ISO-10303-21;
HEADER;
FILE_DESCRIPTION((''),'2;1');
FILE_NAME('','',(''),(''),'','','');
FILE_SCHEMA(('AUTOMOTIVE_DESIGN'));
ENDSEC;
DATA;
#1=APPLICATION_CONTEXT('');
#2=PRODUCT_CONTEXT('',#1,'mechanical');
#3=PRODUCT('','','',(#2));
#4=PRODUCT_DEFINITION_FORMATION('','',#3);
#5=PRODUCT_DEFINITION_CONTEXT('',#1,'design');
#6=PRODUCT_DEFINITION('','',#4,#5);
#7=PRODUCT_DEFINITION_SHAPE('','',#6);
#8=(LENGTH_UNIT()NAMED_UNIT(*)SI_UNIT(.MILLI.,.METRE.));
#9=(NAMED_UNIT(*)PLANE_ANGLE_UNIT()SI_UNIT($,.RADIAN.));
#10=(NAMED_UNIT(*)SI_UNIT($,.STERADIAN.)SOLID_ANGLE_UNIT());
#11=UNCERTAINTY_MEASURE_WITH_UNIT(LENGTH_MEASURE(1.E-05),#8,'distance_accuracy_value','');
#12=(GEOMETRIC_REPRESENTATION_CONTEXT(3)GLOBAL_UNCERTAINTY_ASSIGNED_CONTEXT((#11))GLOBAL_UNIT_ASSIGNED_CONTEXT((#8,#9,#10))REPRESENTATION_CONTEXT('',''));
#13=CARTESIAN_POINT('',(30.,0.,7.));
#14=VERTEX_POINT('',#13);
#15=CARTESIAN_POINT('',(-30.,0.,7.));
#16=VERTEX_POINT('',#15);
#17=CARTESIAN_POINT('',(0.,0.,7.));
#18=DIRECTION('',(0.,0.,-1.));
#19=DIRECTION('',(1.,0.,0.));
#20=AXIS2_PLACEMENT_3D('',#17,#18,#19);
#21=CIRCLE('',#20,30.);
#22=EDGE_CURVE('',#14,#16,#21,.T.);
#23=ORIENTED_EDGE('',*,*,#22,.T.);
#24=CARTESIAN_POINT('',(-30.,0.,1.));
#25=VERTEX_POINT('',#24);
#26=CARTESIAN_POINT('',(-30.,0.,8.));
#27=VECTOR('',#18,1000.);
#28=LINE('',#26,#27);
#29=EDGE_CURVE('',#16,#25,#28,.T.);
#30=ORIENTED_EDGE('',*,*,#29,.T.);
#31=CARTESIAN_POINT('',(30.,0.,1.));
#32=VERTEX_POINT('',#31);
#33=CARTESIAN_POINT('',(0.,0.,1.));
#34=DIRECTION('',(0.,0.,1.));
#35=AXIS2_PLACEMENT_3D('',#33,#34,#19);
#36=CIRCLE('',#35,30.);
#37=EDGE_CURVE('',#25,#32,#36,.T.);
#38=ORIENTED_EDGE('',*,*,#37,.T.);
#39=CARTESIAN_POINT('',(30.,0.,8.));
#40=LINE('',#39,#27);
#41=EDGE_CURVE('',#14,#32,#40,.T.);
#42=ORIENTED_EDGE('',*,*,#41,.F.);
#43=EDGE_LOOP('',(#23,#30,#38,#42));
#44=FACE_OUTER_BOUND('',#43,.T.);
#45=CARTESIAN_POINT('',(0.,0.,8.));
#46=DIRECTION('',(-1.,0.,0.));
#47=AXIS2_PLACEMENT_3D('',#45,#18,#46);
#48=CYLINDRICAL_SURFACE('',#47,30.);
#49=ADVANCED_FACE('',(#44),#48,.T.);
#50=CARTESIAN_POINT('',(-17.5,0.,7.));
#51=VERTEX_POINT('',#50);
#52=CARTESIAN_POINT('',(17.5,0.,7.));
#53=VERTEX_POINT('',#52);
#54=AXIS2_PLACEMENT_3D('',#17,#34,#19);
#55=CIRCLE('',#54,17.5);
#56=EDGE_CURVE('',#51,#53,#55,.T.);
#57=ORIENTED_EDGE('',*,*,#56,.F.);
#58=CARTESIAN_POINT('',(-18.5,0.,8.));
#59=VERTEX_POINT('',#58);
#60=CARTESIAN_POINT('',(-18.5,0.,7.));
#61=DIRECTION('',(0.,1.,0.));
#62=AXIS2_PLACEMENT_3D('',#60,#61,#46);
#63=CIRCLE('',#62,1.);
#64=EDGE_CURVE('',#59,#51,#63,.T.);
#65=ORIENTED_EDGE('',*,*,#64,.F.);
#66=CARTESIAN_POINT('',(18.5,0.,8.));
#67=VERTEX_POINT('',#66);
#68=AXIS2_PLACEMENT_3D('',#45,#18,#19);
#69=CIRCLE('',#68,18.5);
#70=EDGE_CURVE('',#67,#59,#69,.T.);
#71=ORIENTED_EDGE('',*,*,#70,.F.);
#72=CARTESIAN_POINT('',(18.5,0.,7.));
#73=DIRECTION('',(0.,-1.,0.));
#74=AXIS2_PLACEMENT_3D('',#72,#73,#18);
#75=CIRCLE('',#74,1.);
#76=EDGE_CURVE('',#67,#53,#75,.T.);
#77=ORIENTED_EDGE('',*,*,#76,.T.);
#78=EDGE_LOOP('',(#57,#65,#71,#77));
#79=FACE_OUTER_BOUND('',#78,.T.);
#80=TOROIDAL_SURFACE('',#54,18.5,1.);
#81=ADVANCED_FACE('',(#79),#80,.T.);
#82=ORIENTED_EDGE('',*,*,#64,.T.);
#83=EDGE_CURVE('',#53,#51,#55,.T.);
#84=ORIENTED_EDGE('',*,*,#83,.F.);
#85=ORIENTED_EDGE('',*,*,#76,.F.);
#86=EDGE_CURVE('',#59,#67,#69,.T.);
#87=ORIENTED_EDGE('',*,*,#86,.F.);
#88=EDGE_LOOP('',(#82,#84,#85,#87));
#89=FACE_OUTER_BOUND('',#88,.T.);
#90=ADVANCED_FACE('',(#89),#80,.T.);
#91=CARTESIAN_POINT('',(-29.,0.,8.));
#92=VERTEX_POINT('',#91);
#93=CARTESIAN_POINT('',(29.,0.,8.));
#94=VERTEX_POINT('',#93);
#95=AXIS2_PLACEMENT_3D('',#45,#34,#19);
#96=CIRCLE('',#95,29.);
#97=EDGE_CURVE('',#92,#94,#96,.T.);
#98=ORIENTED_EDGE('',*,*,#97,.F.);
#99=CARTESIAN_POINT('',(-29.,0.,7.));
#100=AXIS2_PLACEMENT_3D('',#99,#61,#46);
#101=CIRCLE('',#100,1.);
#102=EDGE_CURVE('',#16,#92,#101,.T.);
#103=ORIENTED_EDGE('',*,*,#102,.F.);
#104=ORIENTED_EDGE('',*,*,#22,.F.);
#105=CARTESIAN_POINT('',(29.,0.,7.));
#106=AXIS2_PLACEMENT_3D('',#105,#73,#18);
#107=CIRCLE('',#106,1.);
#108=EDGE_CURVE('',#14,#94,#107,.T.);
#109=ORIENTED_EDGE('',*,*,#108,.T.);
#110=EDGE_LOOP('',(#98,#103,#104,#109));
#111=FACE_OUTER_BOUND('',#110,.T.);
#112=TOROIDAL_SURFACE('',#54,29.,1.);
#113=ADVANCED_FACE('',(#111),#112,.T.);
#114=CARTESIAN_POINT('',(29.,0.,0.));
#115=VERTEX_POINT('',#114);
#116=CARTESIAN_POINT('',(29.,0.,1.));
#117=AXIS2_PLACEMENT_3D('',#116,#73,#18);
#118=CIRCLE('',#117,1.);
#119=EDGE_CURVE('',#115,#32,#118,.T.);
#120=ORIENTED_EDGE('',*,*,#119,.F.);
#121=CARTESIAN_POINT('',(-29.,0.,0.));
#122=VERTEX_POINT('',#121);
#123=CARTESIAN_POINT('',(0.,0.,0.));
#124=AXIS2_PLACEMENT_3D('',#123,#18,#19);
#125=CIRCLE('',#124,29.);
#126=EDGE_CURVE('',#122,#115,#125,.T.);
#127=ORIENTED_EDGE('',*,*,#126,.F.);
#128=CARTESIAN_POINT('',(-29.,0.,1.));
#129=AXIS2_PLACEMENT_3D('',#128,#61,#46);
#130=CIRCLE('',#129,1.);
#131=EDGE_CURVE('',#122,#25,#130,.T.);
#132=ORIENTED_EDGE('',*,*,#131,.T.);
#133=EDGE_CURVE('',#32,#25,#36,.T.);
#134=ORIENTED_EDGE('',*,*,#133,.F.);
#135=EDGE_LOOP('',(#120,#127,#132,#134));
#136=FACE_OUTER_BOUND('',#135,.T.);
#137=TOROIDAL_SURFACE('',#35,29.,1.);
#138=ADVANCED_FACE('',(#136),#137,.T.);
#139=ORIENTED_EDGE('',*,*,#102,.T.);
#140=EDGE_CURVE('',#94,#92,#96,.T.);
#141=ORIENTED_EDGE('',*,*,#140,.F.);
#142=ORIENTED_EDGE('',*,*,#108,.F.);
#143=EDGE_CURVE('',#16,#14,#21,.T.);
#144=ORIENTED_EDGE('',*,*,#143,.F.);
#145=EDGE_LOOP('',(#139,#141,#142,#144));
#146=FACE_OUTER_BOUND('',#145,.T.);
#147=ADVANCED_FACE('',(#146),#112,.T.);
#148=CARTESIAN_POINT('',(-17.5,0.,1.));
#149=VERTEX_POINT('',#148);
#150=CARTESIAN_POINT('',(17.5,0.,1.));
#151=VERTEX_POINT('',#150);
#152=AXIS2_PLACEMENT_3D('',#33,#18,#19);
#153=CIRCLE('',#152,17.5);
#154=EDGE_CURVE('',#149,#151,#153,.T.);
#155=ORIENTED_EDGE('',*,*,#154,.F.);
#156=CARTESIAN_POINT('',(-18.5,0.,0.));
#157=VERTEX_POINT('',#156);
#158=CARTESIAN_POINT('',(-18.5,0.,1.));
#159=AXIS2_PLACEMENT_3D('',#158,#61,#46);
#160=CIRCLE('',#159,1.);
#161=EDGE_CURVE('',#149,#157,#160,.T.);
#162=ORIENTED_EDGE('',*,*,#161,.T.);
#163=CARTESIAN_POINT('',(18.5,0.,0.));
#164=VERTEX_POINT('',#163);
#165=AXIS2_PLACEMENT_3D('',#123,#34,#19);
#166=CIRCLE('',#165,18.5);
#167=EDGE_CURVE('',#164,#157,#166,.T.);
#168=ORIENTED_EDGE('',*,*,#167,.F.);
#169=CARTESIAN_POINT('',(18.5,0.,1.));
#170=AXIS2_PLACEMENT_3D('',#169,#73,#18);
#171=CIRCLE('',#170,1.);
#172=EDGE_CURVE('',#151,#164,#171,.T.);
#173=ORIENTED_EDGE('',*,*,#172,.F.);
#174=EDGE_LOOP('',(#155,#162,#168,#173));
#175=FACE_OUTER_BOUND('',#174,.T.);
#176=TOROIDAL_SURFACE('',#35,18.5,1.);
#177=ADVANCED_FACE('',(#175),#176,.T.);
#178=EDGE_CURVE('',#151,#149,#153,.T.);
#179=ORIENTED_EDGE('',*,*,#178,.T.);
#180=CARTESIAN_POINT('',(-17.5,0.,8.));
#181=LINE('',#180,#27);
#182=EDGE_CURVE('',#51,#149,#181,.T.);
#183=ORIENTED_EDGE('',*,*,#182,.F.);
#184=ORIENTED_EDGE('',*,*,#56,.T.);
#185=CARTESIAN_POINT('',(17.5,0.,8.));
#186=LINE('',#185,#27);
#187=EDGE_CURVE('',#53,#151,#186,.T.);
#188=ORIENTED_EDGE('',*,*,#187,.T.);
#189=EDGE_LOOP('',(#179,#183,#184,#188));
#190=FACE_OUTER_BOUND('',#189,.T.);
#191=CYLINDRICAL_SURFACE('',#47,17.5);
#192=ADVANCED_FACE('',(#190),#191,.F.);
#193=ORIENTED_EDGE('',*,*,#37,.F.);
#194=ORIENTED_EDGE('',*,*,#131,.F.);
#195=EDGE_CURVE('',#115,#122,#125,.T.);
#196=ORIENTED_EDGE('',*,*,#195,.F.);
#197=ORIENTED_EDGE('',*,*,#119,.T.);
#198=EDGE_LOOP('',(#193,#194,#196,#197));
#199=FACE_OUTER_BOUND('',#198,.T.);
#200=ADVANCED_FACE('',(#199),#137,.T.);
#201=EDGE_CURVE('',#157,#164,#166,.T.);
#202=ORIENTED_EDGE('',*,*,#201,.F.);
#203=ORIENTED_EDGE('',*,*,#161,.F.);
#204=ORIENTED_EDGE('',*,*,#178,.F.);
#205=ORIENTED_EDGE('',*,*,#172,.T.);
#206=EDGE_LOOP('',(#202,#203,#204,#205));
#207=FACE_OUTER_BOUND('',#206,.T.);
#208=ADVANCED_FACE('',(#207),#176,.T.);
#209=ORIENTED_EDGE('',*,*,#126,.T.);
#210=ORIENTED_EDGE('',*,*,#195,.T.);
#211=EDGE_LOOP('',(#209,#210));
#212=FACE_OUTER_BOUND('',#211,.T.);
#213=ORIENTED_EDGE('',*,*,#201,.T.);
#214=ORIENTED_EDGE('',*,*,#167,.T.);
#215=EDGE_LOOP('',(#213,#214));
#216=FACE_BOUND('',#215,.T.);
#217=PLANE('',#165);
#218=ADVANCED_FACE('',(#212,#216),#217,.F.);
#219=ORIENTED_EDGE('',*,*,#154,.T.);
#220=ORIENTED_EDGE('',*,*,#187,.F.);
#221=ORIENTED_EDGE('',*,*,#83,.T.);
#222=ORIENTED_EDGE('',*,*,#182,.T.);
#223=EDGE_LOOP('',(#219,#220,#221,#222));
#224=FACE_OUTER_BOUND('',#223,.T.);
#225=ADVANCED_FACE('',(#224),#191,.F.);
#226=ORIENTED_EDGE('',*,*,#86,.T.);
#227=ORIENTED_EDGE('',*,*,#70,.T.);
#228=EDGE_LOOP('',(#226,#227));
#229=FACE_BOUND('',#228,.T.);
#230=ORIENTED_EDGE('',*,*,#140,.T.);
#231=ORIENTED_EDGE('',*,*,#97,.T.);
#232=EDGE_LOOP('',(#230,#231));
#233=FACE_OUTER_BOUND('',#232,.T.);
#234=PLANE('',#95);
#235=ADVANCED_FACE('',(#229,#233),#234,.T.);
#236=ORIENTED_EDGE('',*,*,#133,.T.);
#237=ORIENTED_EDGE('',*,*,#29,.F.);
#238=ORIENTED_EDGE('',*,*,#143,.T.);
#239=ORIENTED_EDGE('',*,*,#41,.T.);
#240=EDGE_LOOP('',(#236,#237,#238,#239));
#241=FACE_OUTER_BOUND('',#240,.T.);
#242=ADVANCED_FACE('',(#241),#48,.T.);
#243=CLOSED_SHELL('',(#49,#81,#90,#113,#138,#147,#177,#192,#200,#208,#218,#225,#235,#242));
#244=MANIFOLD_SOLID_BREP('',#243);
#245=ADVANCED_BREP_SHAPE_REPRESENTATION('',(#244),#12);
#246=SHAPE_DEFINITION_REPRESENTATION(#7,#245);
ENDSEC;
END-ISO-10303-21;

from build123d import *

# Parameters (mm, degrees)
SKETCH_1_R      = 30
SKETCH_1_R_2    = 17.5
EXTRUDE_1_DEPTH = 8
FILLET_1_R      = 1


with BuildPart() as part:
    # 草图1 → 凸台-拉伸1 (new body)
    with BuildSketch(Plane.XY):
        Circle(SKETCH_1_R)
        Circle(SKETCH_1_R_2, mode=Mode.SUBTRACT)
    extrude(amount=EXTRUDE_1_DEPTH)

    # 圆角1
    fillet_1_edges = [part.edges().sort_by_distance(p)[0] for p in [
        (-30, 0, 0),
        (-30, 0, 8),
        (-17.5, 0, 0),
        (-17.5, 0, 8),
    ]]
    fillet(fillet_1_edges, radius=FILLET_1_R)


solid = part.part
